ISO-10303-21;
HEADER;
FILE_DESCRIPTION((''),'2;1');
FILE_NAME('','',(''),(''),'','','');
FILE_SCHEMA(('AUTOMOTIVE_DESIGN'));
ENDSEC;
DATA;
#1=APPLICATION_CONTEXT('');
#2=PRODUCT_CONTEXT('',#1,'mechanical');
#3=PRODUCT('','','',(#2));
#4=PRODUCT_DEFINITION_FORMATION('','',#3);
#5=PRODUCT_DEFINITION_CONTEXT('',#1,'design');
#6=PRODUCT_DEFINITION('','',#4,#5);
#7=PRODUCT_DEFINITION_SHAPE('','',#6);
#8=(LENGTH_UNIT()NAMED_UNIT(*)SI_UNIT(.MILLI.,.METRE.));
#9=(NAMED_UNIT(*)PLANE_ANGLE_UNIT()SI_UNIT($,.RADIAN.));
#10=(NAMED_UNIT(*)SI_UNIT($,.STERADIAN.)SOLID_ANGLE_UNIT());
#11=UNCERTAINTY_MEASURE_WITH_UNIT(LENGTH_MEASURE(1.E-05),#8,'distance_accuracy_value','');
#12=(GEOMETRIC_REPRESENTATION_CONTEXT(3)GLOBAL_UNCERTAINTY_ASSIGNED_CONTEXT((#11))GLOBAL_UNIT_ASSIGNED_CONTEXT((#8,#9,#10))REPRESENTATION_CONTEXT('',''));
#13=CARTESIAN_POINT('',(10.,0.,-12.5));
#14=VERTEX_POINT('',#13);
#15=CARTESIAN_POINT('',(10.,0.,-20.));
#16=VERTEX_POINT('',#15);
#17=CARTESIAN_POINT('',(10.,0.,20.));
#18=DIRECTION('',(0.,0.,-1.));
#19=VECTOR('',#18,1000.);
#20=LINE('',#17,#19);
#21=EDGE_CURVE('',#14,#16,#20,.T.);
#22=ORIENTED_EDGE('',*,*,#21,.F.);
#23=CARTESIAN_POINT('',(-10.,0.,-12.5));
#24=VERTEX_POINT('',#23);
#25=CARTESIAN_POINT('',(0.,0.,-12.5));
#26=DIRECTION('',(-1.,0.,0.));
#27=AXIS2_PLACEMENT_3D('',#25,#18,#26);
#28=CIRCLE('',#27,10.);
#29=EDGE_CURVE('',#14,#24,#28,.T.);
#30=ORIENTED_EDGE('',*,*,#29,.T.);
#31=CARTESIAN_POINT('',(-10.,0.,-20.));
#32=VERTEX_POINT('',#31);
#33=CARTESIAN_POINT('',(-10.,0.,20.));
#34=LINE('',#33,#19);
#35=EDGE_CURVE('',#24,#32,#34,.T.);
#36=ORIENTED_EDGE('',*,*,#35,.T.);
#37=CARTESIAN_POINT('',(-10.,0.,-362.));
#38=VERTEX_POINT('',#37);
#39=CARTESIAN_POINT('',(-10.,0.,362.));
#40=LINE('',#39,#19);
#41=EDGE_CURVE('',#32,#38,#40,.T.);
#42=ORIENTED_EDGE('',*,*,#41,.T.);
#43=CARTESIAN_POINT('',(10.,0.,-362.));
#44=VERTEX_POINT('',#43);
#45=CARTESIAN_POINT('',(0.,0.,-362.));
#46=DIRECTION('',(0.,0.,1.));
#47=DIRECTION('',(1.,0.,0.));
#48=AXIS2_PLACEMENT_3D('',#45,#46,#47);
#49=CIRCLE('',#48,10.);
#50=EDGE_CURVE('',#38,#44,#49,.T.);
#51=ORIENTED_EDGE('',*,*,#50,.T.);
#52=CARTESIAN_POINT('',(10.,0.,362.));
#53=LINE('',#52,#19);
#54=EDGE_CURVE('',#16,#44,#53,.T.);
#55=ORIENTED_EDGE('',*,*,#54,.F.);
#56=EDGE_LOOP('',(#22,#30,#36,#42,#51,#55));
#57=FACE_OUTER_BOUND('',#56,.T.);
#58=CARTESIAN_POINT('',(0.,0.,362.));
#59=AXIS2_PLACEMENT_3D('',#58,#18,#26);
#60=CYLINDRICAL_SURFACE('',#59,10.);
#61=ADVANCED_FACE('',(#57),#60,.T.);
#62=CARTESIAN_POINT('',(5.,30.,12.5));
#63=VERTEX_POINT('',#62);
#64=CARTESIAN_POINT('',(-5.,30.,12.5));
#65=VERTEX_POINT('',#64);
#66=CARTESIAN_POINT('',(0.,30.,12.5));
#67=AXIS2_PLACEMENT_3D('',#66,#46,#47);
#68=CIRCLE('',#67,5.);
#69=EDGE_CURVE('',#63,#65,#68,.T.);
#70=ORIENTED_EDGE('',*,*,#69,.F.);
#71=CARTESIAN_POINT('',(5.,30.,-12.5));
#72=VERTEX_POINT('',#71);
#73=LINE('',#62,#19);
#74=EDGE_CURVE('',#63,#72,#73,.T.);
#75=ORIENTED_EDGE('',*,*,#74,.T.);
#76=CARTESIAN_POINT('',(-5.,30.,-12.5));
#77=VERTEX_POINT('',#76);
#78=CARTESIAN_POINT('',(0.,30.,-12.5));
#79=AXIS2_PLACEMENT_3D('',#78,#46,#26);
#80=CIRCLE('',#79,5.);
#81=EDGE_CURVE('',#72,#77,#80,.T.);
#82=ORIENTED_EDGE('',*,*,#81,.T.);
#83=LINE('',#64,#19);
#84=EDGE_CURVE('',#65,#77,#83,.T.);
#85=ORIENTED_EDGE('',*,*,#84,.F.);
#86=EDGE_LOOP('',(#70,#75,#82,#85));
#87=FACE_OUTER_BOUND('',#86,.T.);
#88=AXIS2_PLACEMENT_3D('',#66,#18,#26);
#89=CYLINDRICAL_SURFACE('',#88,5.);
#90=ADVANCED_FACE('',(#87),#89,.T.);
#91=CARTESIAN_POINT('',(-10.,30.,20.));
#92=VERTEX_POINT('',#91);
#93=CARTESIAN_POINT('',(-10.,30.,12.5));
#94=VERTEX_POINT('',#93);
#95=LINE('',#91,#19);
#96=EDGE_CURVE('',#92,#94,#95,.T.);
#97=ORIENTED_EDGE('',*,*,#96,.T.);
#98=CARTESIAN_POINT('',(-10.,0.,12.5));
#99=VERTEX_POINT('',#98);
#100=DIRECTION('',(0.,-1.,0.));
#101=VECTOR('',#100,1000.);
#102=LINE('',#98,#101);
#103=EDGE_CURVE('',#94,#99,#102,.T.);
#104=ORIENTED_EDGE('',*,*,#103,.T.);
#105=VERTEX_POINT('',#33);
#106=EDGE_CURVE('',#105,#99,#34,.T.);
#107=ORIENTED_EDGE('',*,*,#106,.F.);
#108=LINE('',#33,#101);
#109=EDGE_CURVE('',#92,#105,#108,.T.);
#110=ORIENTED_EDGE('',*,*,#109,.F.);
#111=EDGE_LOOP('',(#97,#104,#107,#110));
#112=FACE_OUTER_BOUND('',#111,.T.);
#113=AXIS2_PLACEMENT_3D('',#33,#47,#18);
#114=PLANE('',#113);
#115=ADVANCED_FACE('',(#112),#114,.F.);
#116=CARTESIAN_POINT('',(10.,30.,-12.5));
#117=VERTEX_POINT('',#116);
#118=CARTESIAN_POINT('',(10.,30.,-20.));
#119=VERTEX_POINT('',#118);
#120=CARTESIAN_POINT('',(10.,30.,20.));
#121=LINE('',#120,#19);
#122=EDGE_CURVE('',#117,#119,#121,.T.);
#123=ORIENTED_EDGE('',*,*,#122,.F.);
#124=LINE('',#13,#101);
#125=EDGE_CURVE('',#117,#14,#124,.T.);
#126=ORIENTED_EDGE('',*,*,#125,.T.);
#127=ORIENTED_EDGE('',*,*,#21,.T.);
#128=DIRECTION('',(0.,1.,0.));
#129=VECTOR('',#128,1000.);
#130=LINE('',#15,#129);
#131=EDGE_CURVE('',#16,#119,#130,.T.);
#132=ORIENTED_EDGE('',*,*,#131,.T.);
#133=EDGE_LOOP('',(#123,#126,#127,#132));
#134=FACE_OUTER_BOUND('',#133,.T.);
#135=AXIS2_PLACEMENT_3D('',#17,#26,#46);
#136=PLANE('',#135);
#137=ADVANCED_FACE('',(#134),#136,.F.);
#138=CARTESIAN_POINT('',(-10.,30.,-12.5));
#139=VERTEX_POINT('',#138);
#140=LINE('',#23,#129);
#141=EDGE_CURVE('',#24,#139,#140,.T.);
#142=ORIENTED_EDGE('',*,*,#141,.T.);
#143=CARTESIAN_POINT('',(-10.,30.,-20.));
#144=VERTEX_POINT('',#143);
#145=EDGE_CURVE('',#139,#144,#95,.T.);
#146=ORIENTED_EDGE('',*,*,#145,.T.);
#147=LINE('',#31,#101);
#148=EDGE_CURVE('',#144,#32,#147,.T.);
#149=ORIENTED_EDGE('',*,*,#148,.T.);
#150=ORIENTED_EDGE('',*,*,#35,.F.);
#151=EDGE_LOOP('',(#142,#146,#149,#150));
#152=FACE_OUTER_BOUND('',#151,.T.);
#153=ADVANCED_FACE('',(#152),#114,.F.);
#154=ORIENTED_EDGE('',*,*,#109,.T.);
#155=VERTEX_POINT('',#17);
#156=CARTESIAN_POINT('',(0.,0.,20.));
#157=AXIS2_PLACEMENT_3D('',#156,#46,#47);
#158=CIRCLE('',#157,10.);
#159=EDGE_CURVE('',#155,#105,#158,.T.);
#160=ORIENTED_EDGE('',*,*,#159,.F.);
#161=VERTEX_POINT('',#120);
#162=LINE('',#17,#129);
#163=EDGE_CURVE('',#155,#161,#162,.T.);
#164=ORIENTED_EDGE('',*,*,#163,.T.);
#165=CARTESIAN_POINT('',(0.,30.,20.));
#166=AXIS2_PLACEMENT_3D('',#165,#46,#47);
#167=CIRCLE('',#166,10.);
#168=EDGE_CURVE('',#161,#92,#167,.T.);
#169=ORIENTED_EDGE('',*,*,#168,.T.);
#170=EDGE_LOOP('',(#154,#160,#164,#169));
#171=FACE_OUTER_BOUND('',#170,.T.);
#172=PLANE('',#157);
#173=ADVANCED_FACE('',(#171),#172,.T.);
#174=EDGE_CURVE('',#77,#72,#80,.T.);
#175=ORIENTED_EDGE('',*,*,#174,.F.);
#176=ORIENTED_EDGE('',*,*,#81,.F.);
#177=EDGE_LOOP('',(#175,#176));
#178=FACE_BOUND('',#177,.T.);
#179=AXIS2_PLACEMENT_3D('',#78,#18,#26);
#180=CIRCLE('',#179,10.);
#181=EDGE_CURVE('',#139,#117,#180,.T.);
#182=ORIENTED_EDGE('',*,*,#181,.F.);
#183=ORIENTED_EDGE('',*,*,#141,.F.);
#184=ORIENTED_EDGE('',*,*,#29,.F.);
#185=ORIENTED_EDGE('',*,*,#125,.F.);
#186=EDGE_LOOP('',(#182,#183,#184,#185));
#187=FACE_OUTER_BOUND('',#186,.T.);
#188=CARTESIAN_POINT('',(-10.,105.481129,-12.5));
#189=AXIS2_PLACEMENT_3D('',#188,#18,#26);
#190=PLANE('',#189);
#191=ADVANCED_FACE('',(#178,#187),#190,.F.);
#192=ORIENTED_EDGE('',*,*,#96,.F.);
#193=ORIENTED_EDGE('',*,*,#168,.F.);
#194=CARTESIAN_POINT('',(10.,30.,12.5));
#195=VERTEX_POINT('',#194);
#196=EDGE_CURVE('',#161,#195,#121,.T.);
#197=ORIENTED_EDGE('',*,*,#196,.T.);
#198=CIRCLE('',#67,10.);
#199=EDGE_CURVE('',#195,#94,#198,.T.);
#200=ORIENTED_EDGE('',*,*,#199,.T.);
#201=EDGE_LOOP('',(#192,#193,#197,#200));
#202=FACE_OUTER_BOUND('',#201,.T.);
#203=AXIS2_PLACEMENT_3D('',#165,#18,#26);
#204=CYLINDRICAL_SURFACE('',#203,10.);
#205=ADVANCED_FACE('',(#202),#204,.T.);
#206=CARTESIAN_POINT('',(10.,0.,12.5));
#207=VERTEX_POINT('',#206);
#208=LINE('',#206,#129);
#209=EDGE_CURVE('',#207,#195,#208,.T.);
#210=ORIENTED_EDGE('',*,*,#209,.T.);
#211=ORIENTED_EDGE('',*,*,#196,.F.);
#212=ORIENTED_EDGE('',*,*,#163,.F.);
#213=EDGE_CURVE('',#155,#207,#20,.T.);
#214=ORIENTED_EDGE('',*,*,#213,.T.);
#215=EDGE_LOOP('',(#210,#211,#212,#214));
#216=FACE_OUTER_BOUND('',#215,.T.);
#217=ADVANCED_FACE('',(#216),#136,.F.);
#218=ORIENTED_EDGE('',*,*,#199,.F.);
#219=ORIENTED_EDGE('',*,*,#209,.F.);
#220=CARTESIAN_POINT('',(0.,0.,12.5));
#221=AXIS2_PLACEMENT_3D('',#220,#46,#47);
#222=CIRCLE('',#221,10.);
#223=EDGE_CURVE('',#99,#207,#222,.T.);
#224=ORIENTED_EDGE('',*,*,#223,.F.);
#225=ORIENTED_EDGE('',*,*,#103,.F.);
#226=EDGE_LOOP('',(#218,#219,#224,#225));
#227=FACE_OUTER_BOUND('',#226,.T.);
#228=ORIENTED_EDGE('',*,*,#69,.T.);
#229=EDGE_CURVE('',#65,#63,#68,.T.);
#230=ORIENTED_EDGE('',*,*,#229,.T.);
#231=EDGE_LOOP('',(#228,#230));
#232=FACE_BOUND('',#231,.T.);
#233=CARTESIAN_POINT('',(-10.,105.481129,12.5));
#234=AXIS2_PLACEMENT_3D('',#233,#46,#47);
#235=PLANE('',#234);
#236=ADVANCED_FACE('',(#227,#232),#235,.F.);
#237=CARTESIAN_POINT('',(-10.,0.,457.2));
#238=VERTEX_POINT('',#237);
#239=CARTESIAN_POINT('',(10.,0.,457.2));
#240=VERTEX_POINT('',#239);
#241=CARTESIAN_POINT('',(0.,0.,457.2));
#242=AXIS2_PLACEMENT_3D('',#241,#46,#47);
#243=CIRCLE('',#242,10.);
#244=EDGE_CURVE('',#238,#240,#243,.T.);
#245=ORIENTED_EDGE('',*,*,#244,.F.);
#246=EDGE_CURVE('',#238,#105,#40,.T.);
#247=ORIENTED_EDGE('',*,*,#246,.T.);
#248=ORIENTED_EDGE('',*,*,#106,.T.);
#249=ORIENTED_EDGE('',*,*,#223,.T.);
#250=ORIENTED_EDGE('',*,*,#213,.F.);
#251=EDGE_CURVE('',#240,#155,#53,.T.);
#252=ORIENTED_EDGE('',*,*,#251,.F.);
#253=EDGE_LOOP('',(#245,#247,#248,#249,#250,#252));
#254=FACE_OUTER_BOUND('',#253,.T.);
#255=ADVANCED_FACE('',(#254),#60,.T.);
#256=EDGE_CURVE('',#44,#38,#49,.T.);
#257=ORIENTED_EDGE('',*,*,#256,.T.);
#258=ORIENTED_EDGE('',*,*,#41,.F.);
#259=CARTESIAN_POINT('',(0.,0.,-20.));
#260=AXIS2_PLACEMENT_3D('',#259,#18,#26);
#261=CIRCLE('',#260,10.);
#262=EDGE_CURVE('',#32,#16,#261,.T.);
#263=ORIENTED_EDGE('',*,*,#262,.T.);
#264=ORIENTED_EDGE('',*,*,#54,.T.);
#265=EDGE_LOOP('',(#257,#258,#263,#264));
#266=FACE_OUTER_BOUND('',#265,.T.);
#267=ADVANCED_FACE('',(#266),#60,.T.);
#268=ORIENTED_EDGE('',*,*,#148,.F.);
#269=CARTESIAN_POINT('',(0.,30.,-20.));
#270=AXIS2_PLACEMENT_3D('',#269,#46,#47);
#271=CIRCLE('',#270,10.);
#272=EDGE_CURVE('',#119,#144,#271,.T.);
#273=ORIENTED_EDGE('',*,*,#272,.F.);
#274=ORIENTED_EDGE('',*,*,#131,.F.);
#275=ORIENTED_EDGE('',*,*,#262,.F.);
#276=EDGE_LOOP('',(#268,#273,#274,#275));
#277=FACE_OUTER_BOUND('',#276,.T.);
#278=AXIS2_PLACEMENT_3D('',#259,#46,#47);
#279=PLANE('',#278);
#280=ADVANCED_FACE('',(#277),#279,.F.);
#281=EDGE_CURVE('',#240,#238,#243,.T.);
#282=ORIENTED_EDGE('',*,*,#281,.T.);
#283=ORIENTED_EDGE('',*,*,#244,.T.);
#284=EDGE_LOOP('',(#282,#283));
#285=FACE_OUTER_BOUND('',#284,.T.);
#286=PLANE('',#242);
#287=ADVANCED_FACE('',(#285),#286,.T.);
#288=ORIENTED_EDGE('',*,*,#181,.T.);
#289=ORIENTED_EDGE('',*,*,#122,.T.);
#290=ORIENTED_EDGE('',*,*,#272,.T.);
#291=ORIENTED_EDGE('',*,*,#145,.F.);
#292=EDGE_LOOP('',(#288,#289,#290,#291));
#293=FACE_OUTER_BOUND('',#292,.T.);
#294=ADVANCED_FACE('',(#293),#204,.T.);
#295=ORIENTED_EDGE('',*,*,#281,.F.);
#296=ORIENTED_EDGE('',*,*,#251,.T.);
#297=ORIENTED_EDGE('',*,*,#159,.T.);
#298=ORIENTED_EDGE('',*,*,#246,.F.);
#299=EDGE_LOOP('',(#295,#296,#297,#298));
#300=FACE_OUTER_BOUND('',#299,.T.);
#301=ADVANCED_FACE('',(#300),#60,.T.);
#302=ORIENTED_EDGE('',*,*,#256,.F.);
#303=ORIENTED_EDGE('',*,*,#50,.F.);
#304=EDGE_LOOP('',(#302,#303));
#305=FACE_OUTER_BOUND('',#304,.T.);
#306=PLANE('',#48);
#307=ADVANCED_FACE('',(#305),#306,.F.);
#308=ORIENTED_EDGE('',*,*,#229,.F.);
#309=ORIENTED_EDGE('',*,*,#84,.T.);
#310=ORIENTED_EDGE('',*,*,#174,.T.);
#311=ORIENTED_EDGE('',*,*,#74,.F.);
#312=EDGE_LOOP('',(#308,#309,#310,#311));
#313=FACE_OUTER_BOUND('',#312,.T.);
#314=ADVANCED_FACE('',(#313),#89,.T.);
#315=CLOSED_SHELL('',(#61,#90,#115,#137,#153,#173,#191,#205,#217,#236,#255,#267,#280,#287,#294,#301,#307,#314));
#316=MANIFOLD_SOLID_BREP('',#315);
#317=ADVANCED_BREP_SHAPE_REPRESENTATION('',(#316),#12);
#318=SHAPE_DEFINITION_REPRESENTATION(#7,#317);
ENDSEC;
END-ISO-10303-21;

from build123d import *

# Parameters (mm, degrees)
SKETCH1_R               = 10
BOSS_EXTRUDE1_DEPTH     = 362
CUT_EXTRUDE1_DEPTH      = 363.276137773
CUT_EXTRUDE1_DEPTH_BACK = 363.276137773
SKETCH2_W               = 145.080809864
SKETCH2_H               = 40
BOSS_EXTRUDE2_DEPTH     = 20
CUT_EXTRUDE2_DEPTH      = 365.751970522
CUT_EXTRUDE2_DEPTH_BACK = 365.751970522
SKETCH4_W               = 25
SKETCH4_H               = 210.962257982
SKETCH5_R               = 5
BOSS_EXTRUDE3_DEPTH     = 12.5
SKETCH6_R               = 10
BOSS_EXTRUDE4_DEPTH     = 95.2


with BuildPart() as part:
    # Sketch1 → Boss-Extrude1 (new, symmetric)
    with BuildSketch(Plane.XY):
        Circle(SKETCH1_R)
    extrude(amount=BOSS_EXTRUDE1_DEPTH, both=True)

    # Sketch2 → Cut-Extrude1 (cut, two sides: drawn at the far end of the back side and taken through both)
    with BuildSketch(Plane(origin=(0, 0, 0), x_dir=(1, 0, 0), z_dir=(0, 1, 0)).offset(-CUT_EXTRUDE1_DEPTH_BACK)):
        Rectangle(SKETCH2_W, SKETCH2_H)
    extrude(amount=CUT_EXTRUDE1_DEPTH + CUT_EXTRUDE1_DEPTH_BACK, mode=Mode.SUBTRACT)


with BuildPart() as cut_extrude1_piece_1:
    # of the separate pieces the step leaves, piece 1, a body of its own (cut_extrude1_pieces)
    add(part.part.solids().sort_by_distance((10, 0, -362))[0])



with BuildPart() as cut_extrude1_piece_2:
    # of the separate pieces the step leaves, piece 2, a body of its own (cut_extrude1_pieces)
    add(part.part.solids().sort_by_distance((10, 0, 20))[0])


with BuildPart() as cut_extrude1_piece_1_1:
    add(cut_extrude1_piece_1.part)

    add(cut_extrude1_piece_2.part)  # Boss-Extrude2 merges Cut-Extrude1 piece 2
    # Sketch3 → Boss-Extrude2 (add, symmetric)
    with BuildSketch(Plane.XY):
        with BuildLine():
            Line((-10, 0), (-10, 30))
            ThreePointArc((-10, 30), (0, 40), (10, 30))
            Line((10, 30), (10, 0))
            ThreePointArc((10, 0), (0, -10), (-10, 0))
        make_face()
    extrude(amount=BOSS_EXTRUDE2_DEPTH, both=True)

    # Sketch4 → Cut-Extrude2 (cut, two sides: drawn at the far end of the back side and taken through both)
    with BuildSketch(Plane(origin=(10, 0, 0), x_dir=(0, 0, -1), z_dir=(1, 0, 0)).offset(-CUT_EXTRUDE2_DEPTH_BACK)):
        Rectangle(SKETCH4_W, SKETCH4_H)
    extrude(amount=CUT_EXTRUDE2_DEPTH + CUT_EXTRUDE2_DEPTH_BACK, mode=Mode.SUBTRACT)


with BuildPart() as cut_extrude2_piece_1:
    # of the separate pieces the step leaves, piece 1, a body of its own (cut_extrude2_pieces)
    add(cut_extrude1_piece_1_1.part.solids().sort_by_distance((10, 0, 20))[0])



with BuildPart() as cut_extrude2_piece_2:
    # of the separate pieces the step leaves, piece 2, a body of its own (cut_extrude2_pieces)
    add(cut_extrude1_piece_1_1.part.solids().sort_by_distance((10, 0, -20))[0])


with BuildPart() as cut_extrude2_piece_1_1:
    add(cut_extrude2_piece_1.part)

    add(cut_extrude2_piece_2.part)  # Boss-Extrude3 merges Cut-Extrude2 piece 2
    # Sketch5 → Boss-Extrude3 (add, symmetric)
    with BuildSketch(Plane.XY):
        with Locations(Location((0, 30, 0), (0, 0, 180))):
            Circle(SKETCH5_R)
    extrude(amount=BOSS_EXTRUDE3_DEPTH, both=True)

    # Sketch6 → Boss-Extrude4 (add)
    with BuildSketch(Plane.XY.offset(362)):
        Circle(SKETCH6_R)
    extrude(amount=BOSS_EXTRUDE4_DEPTH)


solid = cut_extrude2_piece_1_1.part
